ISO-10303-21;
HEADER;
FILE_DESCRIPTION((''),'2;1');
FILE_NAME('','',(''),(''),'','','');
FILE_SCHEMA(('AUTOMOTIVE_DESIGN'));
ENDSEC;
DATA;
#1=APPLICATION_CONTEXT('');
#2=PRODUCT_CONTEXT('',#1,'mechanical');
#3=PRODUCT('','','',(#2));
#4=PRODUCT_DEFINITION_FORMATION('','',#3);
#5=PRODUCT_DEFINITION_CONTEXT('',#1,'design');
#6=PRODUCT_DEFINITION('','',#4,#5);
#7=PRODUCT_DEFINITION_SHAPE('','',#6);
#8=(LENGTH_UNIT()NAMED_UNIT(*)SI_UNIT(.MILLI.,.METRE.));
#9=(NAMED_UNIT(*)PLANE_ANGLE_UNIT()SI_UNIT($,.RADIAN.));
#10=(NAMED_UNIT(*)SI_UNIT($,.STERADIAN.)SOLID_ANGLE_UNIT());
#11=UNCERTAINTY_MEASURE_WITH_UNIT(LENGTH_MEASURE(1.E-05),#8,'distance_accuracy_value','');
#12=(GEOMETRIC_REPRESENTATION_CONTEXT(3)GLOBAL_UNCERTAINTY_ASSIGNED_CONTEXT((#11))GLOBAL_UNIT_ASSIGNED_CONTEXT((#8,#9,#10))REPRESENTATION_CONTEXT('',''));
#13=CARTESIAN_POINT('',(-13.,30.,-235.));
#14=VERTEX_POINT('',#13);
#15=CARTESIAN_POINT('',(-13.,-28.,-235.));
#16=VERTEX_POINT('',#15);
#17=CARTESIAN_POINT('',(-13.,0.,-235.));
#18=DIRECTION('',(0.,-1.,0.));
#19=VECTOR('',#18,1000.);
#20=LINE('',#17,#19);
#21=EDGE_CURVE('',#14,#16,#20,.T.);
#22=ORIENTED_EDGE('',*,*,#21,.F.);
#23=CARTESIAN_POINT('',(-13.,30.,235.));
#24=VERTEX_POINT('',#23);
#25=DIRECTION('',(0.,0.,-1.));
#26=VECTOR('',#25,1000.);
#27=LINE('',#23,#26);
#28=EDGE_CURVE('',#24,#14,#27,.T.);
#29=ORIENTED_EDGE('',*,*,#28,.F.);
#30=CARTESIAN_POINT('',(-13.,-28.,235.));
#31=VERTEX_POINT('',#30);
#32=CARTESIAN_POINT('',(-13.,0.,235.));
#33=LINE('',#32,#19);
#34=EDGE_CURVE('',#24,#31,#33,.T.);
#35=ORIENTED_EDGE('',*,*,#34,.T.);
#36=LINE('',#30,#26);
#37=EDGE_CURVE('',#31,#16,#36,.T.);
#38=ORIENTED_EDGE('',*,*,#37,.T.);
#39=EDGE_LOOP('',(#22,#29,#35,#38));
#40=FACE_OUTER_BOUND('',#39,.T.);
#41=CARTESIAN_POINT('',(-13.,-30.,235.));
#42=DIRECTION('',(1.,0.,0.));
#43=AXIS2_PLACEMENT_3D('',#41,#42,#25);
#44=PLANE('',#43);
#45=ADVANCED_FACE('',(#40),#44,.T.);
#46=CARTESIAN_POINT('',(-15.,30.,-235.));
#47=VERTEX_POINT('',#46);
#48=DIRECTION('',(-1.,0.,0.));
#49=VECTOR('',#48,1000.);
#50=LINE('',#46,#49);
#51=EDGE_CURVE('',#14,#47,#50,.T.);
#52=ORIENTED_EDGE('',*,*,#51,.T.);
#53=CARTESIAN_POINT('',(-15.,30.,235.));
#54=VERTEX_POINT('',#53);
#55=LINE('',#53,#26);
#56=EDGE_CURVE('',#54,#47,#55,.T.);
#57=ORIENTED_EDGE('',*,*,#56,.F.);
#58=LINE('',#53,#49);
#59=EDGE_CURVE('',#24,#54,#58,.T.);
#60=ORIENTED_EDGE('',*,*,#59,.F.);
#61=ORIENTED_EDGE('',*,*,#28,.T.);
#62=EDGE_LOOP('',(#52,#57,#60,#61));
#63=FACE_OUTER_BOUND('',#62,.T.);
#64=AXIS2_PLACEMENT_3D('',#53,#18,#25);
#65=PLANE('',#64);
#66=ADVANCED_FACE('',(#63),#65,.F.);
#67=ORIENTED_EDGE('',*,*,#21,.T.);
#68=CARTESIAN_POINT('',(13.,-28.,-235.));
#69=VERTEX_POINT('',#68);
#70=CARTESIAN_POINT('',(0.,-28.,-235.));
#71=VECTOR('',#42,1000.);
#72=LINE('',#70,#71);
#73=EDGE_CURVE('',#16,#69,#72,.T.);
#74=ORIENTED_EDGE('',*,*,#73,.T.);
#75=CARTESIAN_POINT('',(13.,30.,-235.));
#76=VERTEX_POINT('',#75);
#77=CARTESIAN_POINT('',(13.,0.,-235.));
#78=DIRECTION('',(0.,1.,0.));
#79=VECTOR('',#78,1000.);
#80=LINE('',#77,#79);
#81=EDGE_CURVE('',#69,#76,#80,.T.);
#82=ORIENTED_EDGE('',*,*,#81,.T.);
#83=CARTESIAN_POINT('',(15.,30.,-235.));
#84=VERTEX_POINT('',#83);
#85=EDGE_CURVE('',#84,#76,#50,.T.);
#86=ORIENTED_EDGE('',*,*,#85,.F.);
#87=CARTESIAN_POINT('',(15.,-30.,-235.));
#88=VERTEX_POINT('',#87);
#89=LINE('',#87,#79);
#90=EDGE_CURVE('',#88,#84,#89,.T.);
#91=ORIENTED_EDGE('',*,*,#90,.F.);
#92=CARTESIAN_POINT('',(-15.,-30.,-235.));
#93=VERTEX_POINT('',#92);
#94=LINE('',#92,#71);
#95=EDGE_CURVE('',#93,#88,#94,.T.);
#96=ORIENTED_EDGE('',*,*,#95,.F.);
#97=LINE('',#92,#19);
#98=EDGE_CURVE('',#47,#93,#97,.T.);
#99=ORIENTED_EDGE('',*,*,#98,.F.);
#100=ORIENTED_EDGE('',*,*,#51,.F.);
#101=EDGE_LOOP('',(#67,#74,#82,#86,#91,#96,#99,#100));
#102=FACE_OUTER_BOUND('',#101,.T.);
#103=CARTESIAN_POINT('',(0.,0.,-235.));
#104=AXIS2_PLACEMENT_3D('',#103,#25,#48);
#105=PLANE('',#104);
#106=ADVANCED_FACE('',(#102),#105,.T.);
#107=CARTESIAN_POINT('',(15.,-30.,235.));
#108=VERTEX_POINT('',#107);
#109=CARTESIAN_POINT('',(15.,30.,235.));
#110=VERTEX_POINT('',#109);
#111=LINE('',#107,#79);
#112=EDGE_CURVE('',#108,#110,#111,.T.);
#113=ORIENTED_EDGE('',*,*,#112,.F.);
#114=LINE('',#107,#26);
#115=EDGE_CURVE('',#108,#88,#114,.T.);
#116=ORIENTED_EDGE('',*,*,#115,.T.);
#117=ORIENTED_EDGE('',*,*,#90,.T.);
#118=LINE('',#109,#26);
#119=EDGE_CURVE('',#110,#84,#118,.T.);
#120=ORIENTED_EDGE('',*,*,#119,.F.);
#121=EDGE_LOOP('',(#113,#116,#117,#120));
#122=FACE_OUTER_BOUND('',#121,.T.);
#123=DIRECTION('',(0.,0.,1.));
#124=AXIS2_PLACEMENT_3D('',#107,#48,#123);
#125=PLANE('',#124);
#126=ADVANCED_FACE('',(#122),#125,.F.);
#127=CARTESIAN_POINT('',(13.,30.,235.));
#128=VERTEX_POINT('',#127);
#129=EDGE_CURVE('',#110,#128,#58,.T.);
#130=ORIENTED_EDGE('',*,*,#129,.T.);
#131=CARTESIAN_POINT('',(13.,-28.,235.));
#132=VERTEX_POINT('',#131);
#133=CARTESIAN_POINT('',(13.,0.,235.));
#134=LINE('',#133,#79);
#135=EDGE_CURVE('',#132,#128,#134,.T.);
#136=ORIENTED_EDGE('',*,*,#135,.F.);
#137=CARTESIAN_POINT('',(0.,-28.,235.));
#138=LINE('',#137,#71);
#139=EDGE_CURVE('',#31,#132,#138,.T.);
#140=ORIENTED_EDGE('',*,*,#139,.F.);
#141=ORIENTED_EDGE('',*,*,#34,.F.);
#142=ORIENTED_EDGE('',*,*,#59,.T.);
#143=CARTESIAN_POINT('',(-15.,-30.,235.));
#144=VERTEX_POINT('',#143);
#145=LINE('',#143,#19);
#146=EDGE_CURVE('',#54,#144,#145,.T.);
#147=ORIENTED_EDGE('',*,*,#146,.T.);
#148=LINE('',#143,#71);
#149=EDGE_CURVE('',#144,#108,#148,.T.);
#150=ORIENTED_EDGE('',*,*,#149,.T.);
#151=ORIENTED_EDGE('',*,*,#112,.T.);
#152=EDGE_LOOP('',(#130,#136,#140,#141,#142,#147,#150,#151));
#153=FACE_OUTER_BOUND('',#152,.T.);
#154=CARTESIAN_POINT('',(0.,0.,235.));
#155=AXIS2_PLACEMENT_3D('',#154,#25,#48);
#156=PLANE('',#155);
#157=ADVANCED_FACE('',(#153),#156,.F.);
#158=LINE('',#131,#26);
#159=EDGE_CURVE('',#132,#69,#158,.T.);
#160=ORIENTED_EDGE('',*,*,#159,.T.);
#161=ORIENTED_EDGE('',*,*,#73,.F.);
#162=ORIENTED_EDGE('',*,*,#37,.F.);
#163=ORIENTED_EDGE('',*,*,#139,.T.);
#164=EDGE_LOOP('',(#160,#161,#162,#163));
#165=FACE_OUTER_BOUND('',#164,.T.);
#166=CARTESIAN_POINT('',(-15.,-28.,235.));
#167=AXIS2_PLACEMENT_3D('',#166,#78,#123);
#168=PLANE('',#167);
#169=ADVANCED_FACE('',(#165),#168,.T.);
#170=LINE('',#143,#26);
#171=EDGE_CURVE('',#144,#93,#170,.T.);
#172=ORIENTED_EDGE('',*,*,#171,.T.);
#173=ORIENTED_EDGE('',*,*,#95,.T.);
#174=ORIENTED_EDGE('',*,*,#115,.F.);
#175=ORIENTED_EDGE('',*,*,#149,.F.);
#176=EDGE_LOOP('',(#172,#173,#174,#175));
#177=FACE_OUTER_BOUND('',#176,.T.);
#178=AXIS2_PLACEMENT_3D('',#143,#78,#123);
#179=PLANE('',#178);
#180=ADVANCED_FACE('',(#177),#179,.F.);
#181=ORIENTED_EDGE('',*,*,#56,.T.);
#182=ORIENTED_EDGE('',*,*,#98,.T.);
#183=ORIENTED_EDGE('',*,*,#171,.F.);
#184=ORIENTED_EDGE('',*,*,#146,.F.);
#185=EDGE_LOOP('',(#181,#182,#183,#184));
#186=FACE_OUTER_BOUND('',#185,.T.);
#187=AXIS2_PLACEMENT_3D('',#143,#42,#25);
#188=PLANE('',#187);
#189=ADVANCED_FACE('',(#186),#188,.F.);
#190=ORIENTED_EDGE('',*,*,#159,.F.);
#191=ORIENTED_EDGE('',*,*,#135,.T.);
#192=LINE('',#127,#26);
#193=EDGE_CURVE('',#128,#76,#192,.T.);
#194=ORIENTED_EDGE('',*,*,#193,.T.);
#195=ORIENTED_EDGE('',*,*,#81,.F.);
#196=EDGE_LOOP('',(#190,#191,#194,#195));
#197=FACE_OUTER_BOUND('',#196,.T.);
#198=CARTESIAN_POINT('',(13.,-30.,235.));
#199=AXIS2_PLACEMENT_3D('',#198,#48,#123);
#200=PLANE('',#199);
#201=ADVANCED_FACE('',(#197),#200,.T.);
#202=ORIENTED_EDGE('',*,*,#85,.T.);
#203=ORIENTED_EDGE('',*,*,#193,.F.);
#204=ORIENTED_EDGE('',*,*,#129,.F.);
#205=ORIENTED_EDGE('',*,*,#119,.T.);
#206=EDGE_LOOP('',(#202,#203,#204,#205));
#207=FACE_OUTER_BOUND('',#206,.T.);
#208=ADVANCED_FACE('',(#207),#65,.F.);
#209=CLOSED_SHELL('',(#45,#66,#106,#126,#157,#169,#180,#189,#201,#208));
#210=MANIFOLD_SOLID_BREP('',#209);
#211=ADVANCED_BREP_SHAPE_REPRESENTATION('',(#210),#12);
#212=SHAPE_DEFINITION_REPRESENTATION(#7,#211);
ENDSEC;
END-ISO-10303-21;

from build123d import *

# Parameters (mm, degrees)
SKETCH_1_W      = 30
SKETCH_1_H      = 60
EXTRUDE_1_DEPTH = 235
SHELL_1_T       = -2


with BuildPart() as part:
    # 草图1 → 凸台-拉伸1 (new, symmetric)
    with BuildSketch(Plane.XY):
        Rectangle(SKETCH_1_W, SKETCH_1_H)
    extrude(amount=EXTRUDE_1_DEPTH, both=True)

    # 抽壳1
    shell_1_openings = [part.faces().sort_by_distance(p)[0] for p in [
        (0, 0, 235),
        (0, 0, -235),
        (0, 30, 0),
    ]]
    offset(amount=SHELL_1_T, openings=shell_1_openings, kind=Kind.INTERSECTION)


solid = part.part
